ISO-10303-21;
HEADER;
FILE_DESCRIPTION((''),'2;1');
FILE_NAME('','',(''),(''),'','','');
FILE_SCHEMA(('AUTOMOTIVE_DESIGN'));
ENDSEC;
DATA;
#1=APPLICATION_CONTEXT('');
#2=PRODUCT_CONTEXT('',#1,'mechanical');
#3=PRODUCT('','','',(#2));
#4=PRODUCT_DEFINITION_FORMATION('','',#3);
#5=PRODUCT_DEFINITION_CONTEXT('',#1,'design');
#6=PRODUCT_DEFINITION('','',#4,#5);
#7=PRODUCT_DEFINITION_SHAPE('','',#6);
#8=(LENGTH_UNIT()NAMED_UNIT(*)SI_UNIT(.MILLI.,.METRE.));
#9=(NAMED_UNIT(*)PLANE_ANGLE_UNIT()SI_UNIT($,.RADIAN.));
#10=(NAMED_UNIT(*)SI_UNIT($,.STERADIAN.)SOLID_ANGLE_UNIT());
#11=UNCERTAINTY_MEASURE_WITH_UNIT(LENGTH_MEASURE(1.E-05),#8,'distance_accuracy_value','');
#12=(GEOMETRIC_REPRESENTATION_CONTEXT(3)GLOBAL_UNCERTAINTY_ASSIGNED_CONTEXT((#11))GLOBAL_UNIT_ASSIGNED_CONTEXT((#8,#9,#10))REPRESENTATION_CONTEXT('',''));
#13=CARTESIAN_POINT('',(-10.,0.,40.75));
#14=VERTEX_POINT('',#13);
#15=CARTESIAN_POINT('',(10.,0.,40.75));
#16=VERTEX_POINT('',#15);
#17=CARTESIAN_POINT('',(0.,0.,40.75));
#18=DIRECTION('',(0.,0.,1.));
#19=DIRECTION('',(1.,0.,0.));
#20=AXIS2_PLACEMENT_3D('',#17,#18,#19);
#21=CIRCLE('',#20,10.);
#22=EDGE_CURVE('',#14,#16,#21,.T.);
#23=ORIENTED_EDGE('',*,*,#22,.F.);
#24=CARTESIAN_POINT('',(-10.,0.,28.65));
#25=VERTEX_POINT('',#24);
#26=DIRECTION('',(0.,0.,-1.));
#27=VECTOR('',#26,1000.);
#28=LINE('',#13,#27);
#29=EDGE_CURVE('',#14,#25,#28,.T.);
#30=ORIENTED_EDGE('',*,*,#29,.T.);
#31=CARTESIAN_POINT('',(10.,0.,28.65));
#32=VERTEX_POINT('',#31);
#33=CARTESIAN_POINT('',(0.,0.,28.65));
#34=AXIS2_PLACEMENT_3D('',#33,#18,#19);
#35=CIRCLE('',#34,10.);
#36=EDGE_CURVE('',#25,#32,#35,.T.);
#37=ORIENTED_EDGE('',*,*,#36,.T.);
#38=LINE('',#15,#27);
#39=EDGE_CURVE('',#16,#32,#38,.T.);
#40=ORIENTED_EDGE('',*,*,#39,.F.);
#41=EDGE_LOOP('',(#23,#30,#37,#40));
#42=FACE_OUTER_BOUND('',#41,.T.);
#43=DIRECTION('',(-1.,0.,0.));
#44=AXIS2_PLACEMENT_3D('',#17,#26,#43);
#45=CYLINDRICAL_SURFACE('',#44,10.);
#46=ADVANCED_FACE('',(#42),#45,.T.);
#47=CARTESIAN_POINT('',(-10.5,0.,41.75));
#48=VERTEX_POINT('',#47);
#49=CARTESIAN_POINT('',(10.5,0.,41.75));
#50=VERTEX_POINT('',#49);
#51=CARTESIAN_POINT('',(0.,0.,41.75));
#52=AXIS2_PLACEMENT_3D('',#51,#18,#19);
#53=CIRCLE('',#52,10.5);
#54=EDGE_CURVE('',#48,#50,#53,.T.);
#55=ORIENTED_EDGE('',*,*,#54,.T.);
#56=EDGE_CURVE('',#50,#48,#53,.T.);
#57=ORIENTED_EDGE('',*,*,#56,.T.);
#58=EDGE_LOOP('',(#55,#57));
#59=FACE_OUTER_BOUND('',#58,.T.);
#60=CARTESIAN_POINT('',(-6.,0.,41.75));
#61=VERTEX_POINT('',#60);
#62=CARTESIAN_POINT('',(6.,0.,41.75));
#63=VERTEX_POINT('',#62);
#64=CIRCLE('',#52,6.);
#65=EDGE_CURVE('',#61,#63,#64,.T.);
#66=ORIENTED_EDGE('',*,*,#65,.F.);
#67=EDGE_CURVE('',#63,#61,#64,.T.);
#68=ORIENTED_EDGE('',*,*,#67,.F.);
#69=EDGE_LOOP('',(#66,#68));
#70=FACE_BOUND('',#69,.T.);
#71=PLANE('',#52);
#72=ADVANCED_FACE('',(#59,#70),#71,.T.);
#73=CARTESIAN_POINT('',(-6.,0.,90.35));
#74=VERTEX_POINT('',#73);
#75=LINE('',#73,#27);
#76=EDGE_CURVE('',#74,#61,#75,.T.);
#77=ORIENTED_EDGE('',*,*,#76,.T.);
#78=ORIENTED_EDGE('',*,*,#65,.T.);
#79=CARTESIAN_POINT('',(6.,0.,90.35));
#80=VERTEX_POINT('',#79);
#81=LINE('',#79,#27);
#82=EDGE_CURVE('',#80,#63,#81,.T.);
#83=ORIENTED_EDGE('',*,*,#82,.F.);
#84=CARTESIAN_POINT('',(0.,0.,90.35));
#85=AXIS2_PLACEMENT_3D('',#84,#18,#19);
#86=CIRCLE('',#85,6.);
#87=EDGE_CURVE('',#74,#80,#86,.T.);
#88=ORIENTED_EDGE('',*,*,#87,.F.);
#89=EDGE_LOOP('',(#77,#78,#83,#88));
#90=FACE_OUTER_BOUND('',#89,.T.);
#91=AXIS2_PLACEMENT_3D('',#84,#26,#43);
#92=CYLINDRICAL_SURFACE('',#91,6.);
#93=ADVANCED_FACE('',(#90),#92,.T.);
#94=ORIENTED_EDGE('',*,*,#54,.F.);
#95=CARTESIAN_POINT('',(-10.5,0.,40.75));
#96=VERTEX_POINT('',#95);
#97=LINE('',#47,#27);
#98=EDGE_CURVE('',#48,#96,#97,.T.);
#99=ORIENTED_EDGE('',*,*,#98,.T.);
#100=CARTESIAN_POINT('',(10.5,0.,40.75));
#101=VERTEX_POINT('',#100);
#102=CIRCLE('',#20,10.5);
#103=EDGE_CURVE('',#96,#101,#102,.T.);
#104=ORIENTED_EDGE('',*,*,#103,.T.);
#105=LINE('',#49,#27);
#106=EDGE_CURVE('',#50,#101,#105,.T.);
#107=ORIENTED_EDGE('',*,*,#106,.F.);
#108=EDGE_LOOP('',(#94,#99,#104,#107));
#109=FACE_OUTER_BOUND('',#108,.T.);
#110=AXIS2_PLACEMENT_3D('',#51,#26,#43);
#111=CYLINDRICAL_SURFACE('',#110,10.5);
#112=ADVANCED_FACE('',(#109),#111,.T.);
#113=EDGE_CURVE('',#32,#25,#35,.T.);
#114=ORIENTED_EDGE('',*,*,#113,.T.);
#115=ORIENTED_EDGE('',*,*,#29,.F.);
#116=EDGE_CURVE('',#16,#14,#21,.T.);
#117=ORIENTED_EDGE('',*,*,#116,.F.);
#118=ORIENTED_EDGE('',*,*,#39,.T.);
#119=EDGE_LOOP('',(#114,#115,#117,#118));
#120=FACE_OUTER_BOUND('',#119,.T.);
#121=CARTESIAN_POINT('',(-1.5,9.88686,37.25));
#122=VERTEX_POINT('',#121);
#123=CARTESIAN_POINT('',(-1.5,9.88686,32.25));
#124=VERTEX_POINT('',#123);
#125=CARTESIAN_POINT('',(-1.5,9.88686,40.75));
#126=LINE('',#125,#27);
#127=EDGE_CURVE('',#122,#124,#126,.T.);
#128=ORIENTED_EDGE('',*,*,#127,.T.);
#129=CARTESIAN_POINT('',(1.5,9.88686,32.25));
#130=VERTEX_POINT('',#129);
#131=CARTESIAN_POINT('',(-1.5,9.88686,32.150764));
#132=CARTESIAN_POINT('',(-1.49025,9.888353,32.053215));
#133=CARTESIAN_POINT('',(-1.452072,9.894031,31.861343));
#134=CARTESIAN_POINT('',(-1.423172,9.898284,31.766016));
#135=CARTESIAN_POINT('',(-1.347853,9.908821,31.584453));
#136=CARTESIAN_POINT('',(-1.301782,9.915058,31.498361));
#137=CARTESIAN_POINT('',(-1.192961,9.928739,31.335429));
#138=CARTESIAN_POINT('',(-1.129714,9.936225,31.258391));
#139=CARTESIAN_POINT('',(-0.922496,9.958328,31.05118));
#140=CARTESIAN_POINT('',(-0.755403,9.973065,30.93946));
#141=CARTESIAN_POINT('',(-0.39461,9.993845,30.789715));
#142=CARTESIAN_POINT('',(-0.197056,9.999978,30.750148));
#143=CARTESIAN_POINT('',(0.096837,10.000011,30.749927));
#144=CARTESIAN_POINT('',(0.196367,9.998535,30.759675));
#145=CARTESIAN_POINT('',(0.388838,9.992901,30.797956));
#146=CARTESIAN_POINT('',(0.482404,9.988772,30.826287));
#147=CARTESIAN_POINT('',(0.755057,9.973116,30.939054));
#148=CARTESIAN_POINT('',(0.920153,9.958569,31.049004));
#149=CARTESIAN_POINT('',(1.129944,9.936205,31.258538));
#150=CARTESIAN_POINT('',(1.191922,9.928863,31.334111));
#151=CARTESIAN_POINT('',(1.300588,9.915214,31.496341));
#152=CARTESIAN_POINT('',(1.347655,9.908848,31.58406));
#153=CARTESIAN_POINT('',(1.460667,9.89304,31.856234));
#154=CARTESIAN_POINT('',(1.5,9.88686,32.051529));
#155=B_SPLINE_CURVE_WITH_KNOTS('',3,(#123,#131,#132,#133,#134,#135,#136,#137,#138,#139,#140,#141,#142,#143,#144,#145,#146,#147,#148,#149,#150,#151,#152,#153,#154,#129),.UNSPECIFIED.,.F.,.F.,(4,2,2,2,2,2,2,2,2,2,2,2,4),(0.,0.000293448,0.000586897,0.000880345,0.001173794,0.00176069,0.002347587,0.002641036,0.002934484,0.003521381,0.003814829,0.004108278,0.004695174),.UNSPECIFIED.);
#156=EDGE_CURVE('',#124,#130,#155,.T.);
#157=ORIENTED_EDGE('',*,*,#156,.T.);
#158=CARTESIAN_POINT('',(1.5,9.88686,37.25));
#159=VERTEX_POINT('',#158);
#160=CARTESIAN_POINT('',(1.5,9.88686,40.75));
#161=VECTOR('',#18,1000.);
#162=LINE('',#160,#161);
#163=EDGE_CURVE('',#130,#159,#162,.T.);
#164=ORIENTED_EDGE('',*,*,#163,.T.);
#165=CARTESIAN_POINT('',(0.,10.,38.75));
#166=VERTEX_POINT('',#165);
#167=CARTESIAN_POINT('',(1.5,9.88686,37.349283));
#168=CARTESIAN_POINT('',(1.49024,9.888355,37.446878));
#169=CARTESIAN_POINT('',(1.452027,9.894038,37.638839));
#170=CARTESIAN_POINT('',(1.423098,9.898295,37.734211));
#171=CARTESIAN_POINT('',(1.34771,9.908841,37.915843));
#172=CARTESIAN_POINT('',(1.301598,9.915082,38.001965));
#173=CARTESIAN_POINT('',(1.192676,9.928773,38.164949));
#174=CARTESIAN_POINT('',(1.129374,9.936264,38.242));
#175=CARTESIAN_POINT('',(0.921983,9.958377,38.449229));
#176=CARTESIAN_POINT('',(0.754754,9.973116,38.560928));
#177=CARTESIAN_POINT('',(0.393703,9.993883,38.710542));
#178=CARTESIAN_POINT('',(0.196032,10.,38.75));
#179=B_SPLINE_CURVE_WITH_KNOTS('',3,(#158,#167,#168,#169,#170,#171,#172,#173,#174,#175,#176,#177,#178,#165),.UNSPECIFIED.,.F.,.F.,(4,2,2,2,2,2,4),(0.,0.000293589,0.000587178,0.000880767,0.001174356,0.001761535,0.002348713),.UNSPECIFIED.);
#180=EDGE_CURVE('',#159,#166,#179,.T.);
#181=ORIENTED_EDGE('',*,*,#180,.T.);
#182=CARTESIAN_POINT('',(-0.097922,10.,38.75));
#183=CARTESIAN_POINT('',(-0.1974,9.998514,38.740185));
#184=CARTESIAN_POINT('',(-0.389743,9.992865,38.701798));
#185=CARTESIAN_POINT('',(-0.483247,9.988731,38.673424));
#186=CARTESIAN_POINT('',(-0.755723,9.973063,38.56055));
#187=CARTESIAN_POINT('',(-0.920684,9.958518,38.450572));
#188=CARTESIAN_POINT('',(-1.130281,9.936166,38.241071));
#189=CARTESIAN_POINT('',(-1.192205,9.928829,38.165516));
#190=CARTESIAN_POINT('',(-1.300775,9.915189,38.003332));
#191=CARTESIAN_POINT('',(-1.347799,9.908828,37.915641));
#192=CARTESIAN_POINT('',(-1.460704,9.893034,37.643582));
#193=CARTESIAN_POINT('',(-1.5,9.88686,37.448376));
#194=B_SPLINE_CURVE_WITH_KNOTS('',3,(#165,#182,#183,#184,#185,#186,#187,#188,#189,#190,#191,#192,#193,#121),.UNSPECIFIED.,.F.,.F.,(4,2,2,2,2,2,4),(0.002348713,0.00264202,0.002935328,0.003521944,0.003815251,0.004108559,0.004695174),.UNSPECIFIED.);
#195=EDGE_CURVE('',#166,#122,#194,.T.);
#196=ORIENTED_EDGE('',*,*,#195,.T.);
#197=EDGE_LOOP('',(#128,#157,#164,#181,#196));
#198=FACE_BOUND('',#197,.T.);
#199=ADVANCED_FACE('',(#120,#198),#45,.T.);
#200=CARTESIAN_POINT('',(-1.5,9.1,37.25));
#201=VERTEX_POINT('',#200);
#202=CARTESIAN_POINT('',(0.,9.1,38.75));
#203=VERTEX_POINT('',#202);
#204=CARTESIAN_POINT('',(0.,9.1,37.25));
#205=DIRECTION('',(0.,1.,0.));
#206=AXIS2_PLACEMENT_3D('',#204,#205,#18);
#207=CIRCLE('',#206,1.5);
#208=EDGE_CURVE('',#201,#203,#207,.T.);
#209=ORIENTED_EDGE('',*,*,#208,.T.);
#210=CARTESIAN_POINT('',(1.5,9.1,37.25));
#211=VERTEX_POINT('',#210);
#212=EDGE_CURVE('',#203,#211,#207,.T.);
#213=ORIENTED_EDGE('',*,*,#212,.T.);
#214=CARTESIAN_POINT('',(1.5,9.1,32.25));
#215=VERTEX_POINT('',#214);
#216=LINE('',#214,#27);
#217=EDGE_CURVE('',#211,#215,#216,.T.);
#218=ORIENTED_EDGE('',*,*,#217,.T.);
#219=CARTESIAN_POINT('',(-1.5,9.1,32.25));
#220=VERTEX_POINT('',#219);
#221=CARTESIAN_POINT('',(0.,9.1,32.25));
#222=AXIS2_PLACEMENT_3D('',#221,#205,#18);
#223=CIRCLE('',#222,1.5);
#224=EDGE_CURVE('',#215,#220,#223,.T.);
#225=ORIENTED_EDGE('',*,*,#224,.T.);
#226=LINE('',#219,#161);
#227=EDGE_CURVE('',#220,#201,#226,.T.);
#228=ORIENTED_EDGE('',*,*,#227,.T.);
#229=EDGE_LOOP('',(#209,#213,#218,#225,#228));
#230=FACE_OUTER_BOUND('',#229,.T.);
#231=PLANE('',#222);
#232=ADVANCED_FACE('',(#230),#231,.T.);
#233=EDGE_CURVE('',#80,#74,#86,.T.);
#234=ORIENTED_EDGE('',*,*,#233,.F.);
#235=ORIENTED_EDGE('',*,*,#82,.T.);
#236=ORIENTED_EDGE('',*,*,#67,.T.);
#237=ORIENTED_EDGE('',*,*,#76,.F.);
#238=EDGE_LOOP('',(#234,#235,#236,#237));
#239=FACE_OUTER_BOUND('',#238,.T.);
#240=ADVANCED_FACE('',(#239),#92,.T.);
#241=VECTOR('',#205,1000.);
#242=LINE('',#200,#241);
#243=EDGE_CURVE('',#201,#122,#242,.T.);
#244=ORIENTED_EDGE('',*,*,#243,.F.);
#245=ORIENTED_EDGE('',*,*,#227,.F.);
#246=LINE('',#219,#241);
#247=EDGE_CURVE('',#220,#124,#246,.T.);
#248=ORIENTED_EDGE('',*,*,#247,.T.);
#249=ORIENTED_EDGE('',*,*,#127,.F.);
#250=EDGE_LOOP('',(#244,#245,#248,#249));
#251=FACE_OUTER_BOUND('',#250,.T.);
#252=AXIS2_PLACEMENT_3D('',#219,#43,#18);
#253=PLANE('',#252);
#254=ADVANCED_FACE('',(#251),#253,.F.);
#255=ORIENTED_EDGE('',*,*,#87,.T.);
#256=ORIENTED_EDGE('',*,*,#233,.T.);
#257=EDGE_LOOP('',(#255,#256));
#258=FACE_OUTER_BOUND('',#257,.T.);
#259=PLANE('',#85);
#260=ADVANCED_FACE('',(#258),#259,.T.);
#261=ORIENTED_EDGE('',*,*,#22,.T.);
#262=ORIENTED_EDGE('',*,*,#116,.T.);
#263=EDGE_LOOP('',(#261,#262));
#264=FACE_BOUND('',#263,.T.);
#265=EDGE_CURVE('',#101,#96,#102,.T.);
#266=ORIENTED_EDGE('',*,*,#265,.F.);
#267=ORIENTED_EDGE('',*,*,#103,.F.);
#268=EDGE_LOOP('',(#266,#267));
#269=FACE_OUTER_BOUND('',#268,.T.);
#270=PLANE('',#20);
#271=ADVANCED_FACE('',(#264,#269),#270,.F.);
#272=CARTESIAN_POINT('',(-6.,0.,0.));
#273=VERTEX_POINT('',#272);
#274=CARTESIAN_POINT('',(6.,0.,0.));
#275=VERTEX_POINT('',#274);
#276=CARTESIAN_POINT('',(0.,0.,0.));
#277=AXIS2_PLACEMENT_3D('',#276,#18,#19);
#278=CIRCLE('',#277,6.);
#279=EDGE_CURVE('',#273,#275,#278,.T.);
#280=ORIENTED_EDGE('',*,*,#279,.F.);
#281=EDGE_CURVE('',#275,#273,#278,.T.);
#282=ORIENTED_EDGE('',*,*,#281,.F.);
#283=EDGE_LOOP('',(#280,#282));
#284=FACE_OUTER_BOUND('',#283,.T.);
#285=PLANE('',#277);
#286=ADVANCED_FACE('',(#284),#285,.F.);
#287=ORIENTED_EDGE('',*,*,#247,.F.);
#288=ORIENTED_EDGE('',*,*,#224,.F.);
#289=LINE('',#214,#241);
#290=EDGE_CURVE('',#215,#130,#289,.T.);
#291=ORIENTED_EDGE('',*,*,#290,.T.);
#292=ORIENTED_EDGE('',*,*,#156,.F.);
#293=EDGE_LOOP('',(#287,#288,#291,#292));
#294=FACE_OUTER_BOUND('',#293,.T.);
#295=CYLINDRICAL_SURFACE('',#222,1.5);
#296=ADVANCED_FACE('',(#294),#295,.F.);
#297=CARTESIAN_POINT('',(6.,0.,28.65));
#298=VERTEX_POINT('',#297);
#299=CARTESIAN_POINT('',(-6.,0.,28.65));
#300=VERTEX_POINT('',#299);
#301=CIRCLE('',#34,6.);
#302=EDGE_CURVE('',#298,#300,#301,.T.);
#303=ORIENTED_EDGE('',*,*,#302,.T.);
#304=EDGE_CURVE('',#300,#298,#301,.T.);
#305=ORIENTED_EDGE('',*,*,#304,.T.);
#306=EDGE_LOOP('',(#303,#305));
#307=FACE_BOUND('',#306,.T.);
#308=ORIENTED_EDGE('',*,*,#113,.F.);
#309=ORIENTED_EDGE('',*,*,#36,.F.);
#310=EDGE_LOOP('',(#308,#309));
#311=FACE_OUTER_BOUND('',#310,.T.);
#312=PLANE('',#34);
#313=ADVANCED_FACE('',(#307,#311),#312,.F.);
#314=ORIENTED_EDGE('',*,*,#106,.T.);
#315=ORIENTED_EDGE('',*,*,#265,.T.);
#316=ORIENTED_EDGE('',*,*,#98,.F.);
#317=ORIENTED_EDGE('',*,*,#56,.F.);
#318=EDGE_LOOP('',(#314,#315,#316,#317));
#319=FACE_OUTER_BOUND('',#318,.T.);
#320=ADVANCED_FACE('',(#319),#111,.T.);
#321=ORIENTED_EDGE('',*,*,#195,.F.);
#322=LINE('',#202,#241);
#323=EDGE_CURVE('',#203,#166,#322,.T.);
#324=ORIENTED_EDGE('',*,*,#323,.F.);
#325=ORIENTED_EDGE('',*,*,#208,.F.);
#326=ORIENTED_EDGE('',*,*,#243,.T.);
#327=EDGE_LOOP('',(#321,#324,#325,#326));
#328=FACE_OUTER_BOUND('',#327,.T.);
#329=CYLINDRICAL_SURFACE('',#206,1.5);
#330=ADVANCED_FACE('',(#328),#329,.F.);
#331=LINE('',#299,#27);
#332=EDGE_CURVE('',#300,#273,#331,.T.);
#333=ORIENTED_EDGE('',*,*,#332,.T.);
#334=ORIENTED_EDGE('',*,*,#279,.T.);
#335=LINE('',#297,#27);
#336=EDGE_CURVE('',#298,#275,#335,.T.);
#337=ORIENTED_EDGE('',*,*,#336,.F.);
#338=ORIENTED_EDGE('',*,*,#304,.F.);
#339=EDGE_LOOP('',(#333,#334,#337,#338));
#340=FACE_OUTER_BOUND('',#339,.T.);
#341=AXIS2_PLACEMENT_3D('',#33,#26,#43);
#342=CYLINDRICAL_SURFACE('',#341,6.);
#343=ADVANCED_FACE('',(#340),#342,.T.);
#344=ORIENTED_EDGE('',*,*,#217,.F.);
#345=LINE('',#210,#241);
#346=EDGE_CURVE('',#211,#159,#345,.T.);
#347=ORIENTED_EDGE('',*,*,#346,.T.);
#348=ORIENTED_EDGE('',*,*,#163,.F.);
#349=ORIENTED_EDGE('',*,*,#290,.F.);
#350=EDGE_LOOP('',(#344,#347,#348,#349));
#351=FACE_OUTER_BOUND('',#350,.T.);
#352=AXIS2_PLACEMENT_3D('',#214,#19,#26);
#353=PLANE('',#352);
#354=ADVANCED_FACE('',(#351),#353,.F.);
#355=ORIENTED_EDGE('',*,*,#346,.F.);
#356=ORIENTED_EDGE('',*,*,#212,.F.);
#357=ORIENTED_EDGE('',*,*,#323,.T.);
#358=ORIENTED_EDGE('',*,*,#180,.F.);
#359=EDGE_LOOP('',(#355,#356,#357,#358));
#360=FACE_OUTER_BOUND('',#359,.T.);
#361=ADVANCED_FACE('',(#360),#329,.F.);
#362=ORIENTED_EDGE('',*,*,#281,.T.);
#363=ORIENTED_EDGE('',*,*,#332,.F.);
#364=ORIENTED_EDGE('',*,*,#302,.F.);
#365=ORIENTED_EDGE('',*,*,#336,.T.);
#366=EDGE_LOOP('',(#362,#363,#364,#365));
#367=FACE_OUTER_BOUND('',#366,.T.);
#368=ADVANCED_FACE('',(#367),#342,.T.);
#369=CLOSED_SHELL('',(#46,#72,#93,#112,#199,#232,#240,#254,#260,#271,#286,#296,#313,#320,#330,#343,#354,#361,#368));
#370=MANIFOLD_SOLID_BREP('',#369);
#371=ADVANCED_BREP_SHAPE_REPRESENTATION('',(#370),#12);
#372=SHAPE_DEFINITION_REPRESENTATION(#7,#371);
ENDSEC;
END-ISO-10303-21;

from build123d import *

# Parameters (mm, degrees)
SKETCH1_R           = 6
BOSS_EXTRUDE1_DEPTH = 28.65
SKETCH2_R           = 10
BOSS_EXTRUDE2_DEPTH = 12.1
SKETCH3_R           = 10.5
BOSS_EXTRUDE3_DEPTH = 1
SKETCH4_R           = 6
BOSS_EXTRUDE4_DEPTH = 48.6
CUT_EXTRUDE1_DEPTH  = 0.9


with BuildPart() as part:
    # Sketch1 → Boss-Extrude1 (new body)
    with BuildSketch(Plane.XY):
        Circle(SKETCH1_R)
    extrude(amount=BOSS_EXTRUDE1_DEPTH)

    # Sketch2 → Boss-Extrude2 (add)
    with BuildSketch(Plane.XY.offset(28.65)):
        Circle(SKETCH2_R)
    extrude(amount=BOSS_EXTRUDE2_DEPTH)

    # Sketch3 → Boss-Extrude3 (add)
    with BuildSketch(Plane.XY.offset(40.75)):
        Circle(SKETCH3_R)
    extrude(amount=BOSS_EXTRUDE3_DEPTH)

    # Sketch4 → Boss-Extrude4 (add)
    with BuildSketch(Plane.XY.offset(41.75)):
        Circle(SKETCH4_R)
    extrude(amount=BOSS_EXTRUDE4_DEPTH)

    # Sketch6 → Cut-Extrude1 (cut, symmetric)
    with BuildSketch(Plane(origin=(0, 10, 0), x_dir=(1, 0, 0), z_dir=(0, 1, 0))):
        with BuildLine():
            Line((1.5, -32.25), (1.5, -37.25))
            ThreePointArc((1.5, -37.25), (0, -38.75), (-1.5, -37.25))
            Line((-1.5, -37.25), (-1.5, -32.25))
            ThreePointArc((-1.5, -32.25), (0, -30.75), (1.5, -32.25))
        make_face()
    extrude(amount=CUT_EXTRUDE1_DEPTH, both=True, mode=Mode.SUBTRACT)


solid = part.part
